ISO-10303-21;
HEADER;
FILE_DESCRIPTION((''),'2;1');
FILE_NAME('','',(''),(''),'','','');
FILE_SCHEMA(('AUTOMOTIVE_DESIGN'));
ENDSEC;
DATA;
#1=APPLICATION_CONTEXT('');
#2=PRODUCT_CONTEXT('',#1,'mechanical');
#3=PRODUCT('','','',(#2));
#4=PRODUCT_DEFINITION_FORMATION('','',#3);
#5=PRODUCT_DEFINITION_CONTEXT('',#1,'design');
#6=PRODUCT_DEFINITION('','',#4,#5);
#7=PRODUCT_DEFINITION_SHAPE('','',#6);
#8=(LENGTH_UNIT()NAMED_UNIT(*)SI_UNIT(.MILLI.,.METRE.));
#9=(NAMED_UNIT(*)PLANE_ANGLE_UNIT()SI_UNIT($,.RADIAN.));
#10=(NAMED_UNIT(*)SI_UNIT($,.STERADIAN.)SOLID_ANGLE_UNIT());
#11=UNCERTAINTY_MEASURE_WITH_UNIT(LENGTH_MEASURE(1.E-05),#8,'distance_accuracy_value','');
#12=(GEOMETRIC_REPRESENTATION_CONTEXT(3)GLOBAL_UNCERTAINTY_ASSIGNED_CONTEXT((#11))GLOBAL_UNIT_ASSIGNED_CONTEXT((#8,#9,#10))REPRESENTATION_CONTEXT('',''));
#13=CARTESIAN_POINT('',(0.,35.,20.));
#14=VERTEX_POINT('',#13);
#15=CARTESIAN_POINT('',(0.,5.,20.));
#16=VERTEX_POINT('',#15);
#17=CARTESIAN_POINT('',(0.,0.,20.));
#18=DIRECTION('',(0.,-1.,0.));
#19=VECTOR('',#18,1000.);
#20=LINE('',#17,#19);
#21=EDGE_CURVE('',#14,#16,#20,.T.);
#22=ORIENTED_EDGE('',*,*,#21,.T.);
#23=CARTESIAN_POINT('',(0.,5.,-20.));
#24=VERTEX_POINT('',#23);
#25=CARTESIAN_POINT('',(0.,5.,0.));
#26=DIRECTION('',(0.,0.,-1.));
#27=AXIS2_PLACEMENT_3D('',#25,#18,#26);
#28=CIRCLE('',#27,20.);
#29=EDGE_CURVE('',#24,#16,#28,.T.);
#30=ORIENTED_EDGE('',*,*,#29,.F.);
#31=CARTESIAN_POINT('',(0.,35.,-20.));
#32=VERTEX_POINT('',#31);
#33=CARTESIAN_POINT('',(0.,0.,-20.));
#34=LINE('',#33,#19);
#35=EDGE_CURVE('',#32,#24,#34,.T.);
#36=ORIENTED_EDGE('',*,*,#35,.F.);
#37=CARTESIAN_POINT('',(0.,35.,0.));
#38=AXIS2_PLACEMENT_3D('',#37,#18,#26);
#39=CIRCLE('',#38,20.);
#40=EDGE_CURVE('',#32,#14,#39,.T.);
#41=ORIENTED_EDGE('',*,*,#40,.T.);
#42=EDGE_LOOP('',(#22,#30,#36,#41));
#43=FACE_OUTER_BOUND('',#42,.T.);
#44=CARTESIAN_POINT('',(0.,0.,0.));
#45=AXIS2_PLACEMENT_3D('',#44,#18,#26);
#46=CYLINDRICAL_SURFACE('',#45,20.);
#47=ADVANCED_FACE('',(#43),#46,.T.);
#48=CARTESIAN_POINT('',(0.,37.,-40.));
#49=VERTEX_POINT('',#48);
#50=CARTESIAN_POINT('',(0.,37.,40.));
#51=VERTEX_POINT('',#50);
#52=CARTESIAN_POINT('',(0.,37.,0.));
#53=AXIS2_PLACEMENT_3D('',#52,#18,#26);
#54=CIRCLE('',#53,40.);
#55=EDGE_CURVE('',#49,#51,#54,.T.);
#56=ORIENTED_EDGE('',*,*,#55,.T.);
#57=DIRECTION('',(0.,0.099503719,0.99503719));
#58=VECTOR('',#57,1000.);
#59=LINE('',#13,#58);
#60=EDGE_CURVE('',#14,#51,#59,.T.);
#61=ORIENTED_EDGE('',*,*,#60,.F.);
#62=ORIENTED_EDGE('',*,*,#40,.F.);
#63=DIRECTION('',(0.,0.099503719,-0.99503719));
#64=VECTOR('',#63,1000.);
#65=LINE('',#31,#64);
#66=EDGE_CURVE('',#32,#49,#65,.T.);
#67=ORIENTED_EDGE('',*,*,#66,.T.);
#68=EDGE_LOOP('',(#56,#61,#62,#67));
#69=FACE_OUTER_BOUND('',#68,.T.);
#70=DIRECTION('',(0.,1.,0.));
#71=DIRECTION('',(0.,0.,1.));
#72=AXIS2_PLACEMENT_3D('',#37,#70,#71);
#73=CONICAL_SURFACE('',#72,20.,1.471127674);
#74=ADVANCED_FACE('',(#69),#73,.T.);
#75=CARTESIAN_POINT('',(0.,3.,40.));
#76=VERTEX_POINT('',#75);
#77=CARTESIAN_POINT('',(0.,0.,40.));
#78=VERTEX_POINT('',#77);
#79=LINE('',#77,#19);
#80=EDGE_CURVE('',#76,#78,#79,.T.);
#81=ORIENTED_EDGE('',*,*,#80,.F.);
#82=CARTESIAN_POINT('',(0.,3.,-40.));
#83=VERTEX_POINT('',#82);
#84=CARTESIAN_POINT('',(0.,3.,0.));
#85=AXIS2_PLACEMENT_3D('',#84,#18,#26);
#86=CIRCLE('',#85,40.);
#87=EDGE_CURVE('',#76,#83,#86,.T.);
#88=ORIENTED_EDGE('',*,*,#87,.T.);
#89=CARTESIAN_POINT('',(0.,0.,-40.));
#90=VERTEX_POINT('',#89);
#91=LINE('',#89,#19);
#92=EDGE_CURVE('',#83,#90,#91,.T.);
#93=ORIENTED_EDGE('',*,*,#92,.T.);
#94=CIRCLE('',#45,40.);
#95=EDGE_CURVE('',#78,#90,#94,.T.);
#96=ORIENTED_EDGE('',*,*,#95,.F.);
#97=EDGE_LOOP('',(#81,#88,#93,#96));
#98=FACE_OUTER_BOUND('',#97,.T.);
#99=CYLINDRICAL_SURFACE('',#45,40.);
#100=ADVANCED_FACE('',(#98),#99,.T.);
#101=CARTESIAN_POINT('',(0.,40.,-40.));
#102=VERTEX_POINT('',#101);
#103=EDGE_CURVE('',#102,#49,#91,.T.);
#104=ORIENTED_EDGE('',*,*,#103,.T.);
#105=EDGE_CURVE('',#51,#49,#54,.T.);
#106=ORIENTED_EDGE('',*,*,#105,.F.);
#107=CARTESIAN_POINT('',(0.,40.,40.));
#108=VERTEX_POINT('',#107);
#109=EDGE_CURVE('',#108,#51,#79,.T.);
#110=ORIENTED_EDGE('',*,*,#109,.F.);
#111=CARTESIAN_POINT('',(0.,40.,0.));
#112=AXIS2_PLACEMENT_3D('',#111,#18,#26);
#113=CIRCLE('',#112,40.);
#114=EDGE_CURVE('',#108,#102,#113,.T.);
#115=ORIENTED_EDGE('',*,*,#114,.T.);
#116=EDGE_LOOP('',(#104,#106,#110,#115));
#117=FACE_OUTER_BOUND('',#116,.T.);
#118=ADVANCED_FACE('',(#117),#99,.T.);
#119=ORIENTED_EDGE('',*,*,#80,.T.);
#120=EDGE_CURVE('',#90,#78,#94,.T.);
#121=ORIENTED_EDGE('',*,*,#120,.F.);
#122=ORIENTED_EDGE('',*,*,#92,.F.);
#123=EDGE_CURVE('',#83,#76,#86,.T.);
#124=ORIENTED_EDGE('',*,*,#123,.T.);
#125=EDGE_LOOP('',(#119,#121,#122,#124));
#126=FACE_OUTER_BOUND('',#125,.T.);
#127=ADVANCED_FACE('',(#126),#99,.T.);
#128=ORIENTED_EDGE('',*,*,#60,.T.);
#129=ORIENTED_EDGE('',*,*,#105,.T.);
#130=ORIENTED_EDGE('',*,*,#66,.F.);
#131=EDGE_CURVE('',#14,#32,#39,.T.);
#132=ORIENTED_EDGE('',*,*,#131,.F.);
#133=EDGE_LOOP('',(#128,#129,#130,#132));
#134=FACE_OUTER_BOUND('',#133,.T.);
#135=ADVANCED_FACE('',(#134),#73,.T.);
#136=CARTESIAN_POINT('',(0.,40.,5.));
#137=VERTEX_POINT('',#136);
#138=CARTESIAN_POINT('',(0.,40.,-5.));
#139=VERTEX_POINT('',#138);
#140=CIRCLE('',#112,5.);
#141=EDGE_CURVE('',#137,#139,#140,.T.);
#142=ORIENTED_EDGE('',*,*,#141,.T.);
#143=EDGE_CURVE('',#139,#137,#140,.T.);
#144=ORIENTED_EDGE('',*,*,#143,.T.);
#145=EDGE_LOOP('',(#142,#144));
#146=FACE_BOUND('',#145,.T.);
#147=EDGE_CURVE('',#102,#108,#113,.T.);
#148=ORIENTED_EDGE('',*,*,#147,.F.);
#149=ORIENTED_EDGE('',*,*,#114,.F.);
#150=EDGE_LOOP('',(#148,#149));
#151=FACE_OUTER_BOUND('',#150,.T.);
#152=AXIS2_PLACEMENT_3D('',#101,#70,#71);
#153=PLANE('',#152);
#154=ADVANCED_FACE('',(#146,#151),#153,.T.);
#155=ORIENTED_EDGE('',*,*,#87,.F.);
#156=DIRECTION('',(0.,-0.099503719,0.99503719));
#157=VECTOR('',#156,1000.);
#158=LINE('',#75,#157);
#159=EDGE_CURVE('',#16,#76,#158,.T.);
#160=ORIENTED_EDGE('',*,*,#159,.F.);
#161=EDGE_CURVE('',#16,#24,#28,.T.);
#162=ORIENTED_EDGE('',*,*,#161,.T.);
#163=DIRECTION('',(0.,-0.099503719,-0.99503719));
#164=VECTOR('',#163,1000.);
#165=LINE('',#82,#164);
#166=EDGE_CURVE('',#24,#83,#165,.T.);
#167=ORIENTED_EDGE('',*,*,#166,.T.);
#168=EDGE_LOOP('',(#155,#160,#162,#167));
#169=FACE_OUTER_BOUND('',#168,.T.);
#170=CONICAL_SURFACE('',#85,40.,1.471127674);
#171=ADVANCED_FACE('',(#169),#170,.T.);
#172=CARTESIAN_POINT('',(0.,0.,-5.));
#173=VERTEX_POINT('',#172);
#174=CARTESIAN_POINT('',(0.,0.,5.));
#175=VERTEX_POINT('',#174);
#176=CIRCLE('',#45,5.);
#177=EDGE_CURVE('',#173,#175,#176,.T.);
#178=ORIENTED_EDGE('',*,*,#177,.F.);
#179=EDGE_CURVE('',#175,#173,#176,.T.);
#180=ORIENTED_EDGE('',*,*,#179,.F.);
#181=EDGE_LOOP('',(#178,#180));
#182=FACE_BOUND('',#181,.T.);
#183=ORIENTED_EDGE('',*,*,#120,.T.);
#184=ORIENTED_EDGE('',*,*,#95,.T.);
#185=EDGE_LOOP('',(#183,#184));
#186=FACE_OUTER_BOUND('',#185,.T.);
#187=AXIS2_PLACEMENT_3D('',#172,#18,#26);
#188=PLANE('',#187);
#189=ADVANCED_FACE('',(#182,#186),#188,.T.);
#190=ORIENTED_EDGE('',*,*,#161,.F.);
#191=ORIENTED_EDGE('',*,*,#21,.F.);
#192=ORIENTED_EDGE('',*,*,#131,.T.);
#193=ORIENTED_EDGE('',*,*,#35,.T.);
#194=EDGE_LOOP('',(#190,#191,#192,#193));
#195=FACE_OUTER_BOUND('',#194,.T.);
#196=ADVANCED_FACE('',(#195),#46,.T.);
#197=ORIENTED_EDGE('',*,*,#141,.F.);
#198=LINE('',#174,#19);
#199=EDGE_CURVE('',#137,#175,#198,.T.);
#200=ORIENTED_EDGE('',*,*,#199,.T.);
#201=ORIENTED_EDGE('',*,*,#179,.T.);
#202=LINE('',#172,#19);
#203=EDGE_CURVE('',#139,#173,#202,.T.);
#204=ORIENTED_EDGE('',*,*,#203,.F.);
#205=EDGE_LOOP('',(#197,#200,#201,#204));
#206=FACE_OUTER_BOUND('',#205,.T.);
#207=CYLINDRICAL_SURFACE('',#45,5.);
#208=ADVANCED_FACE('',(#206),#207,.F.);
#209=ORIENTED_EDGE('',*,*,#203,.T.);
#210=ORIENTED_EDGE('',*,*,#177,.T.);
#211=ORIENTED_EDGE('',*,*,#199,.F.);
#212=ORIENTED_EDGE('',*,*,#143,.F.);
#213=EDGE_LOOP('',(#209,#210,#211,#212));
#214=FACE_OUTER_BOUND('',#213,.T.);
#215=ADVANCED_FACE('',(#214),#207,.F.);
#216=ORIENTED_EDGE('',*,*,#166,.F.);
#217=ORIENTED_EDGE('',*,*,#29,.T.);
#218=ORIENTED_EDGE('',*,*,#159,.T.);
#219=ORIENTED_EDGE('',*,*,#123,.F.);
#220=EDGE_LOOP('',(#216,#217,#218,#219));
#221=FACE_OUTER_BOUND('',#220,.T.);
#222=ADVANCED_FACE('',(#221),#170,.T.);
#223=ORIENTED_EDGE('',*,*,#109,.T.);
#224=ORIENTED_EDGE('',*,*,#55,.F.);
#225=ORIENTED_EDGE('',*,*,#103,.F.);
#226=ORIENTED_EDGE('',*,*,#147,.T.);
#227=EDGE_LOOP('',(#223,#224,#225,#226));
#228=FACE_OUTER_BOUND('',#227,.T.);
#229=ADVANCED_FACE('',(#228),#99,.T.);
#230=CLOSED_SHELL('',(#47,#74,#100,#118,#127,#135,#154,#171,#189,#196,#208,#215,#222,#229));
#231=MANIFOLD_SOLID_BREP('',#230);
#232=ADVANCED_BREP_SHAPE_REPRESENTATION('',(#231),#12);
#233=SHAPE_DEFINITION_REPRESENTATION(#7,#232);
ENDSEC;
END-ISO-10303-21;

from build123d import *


with BuildPart() as part:
    # 草图1 → 旋转1 (revolve)
    with BuildSketch(Plane(origin=(0, 0, 0), x_dir=(0, 0, -1), z_dir=(1, 0, 0))):
        Polygon((5, 0), (40, 0), (40, 3), (20, 5), (20, 35), (40, 37), (40, 40), (5, 40), align=None)
    revolve(axis=Axis((0, 0, 0), (0, 1, 0)))


solid = part.part
